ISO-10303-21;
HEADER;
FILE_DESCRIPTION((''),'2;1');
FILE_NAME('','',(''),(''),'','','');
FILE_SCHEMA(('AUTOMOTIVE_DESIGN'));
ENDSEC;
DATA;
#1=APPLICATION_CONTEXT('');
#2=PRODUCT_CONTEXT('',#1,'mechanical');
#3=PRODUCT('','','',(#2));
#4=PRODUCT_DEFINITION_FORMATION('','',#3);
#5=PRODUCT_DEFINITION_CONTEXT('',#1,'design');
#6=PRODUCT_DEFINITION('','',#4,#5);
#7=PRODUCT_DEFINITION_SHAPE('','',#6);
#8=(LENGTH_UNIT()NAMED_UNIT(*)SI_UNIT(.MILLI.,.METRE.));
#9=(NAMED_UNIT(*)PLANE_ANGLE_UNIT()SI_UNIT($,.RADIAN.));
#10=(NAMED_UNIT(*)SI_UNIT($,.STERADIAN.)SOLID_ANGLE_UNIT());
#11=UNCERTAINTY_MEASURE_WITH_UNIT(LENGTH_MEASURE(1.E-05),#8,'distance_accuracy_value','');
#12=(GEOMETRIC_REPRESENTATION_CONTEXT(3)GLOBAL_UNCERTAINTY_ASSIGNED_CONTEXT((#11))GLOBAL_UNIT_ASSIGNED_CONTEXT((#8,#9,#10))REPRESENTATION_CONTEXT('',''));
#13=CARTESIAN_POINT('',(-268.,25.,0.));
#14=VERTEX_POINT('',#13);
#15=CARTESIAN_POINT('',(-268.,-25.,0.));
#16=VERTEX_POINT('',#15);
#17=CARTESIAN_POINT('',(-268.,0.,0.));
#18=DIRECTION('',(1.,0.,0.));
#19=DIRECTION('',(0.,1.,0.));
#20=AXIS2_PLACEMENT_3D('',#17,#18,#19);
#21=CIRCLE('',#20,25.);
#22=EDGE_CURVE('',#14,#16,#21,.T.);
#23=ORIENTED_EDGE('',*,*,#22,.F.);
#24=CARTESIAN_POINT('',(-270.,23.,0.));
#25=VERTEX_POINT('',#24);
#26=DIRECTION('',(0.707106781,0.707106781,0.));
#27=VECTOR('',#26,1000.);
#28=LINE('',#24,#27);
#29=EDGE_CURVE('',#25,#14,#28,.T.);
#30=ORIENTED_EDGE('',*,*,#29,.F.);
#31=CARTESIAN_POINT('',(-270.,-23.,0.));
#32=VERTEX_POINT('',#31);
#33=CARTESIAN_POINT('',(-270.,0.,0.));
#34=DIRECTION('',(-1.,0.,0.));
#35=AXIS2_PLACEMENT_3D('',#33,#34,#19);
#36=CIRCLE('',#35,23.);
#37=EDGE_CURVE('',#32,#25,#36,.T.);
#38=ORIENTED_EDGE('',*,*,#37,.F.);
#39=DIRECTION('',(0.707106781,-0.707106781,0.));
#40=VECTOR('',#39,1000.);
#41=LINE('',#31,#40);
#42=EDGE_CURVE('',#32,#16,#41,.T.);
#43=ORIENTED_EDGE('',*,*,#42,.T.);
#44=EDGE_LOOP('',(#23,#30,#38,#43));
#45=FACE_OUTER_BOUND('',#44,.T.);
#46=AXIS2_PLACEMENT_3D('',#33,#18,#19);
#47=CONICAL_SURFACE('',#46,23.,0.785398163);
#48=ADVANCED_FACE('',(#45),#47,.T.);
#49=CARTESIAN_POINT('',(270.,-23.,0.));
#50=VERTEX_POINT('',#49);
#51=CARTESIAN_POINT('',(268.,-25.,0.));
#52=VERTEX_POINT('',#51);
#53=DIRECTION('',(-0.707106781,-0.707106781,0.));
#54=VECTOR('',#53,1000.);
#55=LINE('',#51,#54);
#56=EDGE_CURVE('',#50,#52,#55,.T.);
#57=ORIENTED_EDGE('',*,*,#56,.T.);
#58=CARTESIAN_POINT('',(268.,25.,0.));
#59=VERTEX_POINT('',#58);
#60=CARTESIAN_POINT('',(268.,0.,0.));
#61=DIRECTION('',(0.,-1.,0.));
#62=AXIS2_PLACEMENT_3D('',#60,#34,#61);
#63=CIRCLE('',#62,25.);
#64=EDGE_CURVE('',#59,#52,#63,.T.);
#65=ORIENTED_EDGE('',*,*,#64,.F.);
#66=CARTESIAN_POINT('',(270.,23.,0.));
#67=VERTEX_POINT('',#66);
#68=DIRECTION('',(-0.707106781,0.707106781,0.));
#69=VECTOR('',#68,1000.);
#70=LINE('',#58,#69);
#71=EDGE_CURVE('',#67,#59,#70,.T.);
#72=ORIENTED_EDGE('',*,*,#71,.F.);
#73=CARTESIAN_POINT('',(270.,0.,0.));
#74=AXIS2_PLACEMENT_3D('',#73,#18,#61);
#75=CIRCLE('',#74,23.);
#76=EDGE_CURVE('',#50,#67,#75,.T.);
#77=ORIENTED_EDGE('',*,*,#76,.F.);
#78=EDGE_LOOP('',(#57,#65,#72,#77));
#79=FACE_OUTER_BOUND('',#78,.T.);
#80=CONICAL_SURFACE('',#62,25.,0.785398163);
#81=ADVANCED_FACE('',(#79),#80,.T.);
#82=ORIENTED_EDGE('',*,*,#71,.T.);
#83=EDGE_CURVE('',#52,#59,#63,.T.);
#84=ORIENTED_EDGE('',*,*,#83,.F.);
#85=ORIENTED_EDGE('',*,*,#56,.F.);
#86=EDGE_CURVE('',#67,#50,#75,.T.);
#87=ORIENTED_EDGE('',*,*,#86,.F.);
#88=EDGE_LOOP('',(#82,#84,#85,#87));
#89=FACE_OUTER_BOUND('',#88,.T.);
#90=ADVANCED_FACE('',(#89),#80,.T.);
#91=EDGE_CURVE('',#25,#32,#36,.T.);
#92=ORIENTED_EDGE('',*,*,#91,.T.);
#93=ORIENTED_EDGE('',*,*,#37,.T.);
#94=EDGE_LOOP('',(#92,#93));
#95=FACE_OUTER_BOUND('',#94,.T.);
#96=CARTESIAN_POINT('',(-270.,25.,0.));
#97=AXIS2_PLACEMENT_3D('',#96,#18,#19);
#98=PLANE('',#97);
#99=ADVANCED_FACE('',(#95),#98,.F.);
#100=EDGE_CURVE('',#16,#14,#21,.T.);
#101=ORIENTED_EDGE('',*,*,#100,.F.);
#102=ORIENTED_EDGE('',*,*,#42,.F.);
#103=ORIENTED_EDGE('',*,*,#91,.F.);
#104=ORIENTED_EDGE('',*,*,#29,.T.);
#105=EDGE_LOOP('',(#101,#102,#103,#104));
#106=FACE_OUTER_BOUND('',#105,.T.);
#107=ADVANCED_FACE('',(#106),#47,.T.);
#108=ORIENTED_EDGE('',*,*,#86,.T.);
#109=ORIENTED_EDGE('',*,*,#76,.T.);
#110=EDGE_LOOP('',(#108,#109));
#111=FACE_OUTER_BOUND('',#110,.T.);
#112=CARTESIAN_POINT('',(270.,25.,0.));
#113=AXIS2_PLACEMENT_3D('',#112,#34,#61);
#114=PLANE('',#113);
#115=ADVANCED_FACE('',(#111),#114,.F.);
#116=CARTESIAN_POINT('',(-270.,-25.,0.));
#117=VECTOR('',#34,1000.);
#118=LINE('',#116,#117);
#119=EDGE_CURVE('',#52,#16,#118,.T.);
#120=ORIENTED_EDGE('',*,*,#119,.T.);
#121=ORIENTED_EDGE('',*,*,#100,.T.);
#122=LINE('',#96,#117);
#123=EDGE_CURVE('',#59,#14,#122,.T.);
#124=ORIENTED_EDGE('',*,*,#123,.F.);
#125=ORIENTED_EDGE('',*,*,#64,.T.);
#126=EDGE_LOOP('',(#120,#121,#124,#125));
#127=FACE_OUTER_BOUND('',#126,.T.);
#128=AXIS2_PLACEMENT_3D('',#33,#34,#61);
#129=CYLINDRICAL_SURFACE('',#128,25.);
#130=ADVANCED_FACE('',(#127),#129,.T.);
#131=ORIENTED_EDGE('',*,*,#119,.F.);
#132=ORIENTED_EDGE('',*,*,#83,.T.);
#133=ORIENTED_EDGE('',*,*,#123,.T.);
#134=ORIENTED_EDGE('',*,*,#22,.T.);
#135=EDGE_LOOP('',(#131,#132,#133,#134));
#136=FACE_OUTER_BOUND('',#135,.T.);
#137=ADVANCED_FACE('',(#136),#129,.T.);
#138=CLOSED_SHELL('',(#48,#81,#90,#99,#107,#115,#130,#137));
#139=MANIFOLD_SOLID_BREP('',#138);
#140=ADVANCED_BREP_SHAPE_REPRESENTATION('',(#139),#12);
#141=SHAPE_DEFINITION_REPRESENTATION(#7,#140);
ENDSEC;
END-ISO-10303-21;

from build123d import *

# Parameters (mm, degrees)
SHAFT_HALF_PROFILE_W   = 540
SHAFT_HALF_PROFILE_H   = 25
END_CHAMFERS_2X45_SIZE = 2


with BuildPart() as part:
    # Shaft Half Profile → Shaft Ø50x540 (revolve)
    with BuildSketch(Plane.XY, mode=Mode.PRIVATE) as shaft_50x540_sk:
        with Locations((0, 12.5)):
            Rectangle(SHAFT_HALF_PROFILE_W, SHAFT_HALF_PROFILE_H)
    revolve(shaft_50x540_sk.sketch.rotate(Axis((-270, 0, 0), (1, 0, 0)), 180), axis=Axis((-270, 0, 0), (1, 0, 0)))

    # End Chamfers 2x45°
    end_chamfers_2x45_edges = [part.edges().sort_by_distance(p)[0] for p in [
        (-270, 25, 0),
        (270, 25, 0),
    ]]
    chamfer(end_chamfers_2x45_edges, length=END_CHAMFERS_2X45_SIZE)


solid = part.part
